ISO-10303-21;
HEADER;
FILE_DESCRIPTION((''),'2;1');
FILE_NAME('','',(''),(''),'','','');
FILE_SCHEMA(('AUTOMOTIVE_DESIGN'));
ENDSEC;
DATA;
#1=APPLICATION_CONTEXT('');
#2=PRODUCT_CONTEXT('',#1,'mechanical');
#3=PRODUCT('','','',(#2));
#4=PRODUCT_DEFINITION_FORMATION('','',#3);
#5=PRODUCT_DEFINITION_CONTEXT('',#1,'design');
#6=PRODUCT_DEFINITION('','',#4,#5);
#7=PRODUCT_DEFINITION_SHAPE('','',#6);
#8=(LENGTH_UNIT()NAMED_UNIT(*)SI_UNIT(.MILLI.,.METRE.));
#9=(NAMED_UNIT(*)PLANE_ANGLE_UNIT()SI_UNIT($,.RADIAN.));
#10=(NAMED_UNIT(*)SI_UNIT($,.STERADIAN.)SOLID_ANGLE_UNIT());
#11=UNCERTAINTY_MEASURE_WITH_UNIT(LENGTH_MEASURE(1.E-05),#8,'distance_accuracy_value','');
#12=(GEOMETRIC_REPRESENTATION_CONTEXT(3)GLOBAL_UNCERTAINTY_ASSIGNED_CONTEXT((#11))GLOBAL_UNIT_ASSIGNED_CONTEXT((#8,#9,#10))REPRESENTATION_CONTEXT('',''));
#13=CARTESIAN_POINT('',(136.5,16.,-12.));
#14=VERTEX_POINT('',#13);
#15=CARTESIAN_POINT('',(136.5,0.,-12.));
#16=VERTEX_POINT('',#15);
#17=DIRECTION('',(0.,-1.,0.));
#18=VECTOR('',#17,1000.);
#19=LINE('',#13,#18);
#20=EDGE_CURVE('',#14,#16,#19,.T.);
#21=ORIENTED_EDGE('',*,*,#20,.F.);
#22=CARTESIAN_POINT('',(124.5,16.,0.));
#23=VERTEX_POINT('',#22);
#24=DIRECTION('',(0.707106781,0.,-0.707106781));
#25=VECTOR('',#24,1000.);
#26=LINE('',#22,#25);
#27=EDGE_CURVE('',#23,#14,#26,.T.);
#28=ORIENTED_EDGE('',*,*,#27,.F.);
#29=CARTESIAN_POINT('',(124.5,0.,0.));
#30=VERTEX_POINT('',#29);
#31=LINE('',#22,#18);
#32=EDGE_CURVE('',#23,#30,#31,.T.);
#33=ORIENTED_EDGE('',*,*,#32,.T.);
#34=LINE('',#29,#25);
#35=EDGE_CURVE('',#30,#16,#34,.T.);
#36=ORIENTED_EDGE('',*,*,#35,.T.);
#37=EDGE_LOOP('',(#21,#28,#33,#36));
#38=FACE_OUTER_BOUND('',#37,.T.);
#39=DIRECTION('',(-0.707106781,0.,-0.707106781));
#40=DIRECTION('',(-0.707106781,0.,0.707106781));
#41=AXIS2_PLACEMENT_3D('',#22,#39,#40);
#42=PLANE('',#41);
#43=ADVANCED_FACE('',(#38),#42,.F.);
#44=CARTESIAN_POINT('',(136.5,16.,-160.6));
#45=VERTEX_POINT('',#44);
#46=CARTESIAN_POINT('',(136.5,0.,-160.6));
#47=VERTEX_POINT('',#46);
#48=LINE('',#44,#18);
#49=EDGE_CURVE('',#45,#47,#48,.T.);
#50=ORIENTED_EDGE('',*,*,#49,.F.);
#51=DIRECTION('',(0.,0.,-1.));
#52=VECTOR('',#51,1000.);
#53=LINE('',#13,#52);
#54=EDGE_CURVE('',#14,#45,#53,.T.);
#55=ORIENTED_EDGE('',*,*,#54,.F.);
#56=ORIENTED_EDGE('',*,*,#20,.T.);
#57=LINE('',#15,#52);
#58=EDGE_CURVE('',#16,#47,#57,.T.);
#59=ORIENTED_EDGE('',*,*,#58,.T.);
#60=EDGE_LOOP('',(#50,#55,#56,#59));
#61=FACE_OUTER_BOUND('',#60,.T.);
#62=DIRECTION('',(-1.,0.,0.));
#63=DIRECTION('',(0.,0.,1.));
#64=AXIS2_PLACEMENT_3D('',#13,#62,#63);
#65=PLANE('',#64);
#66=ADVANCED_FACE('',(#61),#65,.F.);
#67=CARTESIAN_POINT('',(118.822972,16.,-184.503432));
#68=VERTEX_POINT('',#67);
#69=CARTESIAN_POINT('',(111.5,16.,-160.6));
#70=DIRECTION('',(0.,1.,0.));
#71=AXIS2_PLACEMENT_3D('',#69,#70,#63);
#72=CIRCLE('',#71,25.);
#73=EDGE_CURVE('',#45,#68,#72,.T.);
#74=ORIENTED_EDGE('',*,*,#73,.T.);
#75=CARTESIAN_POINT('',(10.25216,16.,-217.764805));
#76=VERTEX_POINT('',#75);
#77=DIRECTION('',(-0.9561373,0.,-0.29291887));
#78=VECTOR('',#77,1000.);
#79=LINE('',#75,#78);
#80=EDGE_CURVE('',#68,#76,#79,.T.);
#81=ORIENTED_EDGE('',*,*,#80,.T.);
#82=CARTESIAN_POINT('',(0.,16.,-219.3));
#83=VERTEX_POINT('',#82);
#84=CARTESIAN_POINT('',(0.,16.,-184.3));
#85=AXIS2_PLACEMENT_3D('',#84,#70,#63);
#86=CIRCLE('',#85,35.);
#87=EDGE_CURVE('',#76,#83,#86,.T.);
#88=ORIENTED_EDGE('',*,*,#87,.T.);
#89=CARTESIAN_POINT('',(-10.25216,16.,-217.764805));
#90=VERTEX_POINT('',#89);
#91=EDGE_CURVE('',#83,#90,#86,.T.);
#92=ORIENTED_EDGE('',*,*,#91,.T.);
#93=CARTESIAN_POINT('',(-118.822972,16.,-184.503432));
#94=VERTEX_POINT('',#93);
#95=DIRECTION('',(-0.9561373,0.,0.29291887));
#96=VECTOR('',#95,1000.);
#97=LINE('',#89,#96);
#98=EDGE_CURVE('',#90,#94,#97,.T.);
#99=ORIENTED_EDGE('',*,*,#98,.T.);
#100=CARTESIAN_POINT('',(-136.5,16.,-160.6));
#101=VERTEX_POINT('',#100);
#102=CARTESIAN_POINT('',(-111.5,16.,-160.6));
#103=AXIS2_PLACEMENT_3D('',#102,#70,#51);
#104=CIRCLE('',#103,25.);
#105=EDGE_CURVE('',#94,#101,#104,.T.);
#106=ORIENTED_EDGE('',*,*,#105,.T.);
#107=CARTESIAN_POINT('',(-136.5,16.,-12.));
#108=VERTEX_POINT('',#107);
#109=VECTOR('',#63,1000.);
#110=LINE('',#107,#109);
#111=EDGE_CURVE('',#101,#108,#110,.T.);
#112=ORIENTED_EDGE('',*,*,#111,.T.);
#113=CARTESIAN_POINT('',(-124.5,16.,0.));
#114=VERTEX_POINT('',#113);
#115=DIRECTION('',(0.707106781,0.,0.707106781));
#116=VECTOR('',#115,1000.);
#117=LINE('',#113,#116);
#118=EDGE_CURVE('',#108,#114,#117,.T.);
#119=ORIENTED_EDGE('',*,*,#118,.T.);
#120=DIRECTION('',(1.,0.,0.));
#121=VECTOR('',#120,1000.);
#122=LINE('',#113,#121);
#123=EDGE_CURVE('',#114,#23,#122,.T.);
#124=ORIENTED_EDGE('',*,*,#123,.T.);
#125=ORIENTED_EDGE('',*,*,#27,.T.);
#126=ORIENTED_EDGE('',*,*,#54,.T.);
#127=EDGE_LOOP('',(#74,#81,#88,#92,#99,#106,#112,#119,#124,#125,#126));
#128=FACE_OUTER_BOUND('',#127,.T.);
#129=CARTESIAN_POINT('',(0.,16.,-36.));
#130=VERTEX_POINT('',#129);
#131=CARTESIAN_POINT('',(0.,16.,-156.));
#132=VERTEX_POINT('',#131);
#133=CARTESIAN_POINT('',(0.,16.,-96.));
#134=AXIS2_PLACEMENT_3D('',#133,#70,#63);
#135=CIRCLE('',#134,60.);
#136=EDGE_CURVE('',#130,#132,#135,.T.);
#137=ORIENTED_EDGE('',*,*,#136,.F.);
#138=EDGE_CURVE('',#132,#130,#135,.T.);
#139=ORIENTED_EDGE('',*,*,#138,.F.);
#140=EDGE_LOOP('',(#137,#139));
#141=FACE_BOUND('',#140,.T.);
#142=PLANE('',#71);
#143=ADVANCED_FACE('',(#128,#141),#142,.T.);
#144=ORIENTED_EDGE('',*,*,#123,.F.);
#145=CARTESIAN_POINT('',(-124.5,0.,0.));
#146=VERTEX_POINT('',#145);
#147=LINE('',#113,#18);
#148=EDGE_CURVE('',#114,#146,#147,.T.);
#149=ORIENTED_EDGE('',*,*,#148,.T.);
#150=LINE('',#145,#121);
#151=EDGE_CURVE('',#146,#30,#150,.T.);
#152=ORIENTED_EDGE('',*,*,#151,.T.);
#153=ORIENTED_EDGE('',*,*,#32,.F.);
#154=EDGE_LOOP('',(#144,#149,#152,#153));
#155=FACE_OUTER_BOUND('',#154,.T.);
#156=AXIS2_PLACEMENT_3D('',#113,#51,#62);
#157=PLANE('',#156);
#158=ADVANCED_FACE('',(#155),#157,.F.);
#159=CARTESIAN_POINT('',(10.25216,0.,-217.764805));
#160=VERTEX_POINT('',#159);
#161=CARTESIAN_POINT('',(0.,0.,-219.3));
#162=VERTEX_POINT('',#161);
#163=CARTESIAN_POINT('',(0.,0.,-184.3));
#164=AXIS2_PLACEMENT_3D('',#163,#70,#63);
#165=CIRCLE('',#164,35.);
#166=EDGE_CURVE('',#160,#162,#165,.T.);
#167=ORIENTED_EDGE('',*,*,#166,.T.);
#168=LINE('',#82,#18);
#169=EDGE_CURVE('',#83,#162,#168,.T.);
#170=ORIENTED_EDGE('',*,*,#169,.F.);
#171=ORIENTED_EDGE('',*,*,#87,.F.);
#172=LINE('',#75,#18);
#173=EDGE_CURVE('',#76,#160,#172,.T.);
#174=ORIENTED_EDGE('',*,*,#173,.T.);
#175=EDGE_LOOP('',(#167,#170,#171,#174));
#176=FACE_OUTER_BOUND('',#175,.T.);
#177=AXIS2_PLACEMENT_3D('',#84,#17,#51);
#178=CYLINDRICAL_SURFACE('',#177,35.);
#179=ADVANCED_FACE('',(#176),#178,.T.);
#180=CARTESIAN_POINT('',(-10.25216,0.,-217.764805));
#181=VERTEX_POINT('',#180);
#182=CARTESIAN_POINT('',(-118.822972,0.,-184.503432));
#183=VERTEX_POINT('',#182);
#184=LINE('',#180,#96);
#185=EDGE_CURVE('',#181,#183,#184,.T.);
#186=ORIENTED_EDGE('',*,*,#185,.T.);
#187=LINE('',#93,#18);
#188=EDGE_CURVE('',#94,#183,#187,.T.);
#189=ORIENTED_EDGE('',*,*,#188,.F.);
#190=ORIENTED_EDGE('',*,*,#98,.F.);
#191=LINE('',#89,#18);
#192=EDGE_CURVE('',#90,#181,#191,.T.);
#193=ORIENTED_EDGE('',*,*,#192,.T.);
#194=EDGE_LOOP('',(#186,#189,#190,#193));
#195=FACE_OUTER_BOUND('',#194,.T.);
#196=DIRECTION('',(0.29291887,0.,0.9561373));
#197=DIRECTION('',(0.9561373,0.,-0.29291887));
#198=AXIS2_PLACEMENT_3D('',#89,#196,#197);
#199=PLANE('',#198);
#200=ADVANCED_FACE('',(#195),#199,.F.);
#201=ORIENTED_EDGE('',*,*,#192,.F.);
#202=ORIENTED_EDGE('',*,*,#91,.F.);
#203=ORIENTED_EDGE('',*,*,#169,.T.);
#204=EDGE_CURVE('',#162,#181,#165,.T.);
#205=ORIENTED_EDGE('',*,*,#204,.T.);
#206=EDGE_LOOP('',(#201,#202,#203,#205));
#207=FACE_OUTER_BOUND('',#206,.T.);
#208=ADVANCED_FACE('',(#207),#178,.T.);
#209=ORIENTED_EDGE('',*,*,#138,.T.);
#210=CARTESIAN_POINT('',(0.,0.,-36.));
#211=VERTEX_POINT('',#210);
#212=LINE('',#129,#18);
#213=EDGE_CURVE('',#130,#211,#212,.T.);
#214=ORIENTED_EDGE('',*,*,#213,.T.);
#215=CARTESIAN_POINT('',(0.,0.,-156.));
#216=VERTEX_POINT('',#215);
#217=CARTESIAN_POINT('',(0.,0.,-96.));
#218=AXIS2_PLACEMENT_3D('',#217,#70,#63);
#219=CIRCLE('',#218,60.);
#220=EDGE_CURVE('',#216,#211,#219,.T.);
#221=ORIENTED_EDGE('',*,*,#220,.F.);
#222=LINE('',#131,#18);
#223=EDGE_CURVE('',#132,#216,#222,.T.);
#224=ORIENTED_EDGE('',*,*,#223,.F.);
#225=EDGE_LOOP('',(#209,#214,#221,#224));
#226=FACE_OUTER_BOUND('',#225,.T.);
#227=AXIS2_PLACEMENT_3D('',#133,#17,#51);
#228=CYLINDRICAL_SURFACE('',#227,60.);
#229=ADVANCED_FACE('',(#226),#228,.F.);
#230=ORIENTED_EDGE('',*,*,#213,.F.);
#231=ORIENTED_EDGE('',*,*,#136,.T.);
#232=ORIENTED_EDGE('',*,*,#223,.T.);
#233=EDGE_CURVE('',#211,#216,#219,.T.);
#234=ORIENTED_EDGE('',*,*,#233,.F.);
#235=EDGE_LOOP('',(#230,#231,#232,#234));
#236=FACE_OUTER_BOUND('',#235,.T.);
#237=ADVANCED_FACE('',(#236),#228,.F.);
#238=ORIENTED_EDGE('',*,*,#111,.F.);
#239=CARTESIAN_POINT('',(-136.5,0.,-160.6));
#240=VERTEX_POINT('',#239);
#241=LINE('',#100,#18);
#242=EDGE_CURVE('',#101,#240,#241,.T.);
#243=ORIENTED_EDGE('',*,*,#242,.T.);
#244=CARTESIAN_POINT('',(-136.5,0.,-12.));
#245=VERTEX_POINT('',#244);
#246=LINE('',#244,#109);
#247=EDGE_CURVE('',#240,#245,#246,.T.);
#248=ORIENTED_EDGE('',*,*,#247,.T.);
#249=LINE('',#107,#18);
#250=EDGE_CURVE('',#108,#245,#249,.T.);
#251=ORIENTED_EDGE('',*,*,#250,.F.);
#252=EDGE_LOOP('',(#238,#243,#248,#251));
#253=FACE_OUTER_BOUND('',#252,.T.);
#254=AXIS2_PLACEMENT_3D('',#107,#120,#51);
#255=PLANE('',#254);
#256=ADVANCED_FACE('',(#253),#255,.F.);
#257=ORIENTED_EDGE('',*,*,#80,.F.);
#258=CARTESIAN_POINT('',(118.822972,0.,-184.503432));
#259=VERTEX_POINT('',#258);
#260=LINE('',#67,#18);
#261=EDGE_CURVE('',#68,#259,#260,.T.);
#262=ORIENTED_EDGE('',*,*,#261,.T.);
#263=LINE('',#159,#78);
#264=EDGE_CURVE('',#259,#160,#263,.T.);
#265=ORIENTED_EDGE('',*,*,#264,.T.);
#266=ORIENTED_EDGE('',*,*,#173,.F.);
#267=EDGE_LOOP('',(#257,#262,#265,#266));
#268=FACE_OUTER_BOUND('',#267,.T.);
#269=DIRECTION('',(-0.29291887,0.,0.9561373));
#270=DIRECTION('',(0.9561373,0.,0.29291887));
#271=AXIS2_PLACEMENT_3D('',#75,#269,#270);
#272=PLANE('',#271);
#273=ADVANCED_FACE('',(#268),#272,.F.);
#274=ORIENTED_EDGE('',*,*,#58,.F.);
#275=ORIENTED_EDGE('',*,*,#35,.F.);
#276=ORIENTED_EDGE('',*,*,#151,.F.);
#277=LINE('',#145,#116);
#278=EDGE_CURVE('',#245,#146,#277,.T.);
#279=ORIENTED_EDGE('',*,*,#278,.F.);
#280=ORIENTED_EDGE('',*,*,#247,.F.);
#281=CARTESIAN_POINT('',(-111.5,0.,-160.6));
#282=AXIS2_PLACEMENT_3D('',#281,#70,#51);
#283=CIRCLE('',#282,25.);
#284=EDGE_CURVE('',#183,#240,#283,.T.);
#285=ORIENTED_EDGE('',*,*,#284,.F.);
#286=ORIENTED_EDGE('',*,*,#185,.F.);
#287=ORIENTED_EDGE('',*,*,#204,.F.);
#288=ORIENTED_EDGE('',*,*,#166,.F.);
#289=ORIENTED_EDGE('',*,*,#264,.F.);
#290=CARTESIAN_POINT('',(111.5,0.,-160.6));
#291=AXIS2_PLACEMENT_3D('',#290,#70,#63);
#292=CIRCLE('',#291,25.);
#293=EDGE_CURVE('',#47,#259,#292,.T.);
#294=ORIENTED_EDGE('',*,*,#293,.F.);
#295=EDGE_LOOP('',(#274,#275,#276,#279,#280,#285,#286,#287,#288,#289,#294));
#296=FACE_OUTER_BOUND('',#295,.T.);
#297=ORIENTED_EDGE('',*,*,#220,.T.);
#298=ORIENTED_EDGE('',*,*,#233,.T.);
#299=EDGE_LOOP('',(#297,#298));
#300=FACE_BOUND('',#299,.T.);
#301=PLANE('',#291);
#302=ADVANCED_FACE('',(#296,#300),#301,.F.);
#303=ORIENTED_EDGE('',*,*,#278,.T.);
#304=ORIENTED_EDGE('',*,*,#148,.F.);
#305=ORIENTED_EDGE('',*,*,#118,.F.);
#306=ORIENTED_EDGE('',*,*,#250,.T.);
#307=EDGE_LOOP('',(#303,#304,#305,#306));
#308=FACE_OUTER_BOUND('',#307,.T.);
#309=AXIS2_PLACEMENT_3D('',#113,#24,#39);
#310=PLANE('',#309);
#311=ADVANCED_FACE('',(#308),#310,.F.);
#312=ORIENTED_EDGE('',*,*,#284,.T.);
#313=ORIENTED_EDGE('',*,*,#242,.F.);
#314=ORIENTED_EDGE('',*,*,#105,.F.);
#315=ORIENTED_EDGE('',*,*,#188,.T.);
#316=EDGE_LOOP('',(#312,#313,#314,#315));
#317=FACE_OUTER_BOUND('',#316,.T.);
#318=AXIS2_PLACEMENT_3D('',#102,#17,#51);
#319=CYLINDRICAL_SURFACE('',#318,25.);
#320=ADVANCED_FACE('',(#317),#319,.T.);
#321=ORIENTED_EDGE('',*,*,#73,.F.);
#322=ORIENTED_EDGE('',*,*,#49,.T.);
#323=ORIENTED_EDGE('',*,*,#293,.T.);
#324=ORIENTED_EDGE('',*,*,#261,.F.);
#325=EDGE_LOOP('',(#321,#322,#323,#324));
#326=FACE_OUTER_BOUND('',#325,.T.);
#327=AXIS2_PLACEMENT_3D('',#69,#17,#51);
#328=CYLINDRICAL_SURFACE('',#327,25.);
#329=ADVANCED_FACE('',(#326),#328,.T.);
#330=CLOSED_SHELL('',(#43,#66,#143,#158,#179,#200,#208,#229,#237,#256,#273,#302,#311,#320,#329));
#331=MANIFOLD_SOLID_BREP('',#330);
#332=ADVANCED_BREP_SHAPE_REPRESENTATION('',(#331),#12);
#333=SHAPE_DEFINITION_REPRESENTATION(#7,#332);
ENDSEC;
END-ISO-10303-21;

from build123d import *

# Parameters (mm, degrees)
SKETCH1_R           = 60
BOSS_EXTRUDE1_DEPTH = 16


with BuildPart() as part:
    # Sketch1 → Boss-Extrude1 (new body)
    with BuildSketch(Plane(origin=(0, 0, 0), x_dir=(1, 0, 0), z_dir=(0, 1, 0))):
        with BuildLine():
            Line((-124.5, 0), (124.5, 0))
            Line((124.5, 0), (136.5, 12))
            Line((136.5, 12), (136.5, 160.6))
            ThreePointArc((136.5, 160.6), (131.600675284, 175.464819311), (118.822971749, 184.503432489))
            Line((118.822971749, 184.503432489), (10.252160448, 217.764805485))
            ThreePointArc((10.252160448, 217.764805485), (0, 219.3), (-10.252160448, 217.764805485))
            Line((-10.252160448, 217.764805485), (-118.822971749, 184.503432489))
            ThreePointArc((-118.822971749, 184.503432489), (-131.600675284, 175.464819311), (-136.5, 160.6))
            Line((-136.5, 160.6), (-136.5, 12))
            Line((-136.5, 12), (-124.5, 0))
        make_face()
        with Locations(Location((0, 96, 0), (0, 0, 270))):
            Circle(SKETCH1_R, mode=Mode.SUBTRACT)
    extrude(amount=BOSS_EXTRUDE1_DEPTH)


solid = part.part
